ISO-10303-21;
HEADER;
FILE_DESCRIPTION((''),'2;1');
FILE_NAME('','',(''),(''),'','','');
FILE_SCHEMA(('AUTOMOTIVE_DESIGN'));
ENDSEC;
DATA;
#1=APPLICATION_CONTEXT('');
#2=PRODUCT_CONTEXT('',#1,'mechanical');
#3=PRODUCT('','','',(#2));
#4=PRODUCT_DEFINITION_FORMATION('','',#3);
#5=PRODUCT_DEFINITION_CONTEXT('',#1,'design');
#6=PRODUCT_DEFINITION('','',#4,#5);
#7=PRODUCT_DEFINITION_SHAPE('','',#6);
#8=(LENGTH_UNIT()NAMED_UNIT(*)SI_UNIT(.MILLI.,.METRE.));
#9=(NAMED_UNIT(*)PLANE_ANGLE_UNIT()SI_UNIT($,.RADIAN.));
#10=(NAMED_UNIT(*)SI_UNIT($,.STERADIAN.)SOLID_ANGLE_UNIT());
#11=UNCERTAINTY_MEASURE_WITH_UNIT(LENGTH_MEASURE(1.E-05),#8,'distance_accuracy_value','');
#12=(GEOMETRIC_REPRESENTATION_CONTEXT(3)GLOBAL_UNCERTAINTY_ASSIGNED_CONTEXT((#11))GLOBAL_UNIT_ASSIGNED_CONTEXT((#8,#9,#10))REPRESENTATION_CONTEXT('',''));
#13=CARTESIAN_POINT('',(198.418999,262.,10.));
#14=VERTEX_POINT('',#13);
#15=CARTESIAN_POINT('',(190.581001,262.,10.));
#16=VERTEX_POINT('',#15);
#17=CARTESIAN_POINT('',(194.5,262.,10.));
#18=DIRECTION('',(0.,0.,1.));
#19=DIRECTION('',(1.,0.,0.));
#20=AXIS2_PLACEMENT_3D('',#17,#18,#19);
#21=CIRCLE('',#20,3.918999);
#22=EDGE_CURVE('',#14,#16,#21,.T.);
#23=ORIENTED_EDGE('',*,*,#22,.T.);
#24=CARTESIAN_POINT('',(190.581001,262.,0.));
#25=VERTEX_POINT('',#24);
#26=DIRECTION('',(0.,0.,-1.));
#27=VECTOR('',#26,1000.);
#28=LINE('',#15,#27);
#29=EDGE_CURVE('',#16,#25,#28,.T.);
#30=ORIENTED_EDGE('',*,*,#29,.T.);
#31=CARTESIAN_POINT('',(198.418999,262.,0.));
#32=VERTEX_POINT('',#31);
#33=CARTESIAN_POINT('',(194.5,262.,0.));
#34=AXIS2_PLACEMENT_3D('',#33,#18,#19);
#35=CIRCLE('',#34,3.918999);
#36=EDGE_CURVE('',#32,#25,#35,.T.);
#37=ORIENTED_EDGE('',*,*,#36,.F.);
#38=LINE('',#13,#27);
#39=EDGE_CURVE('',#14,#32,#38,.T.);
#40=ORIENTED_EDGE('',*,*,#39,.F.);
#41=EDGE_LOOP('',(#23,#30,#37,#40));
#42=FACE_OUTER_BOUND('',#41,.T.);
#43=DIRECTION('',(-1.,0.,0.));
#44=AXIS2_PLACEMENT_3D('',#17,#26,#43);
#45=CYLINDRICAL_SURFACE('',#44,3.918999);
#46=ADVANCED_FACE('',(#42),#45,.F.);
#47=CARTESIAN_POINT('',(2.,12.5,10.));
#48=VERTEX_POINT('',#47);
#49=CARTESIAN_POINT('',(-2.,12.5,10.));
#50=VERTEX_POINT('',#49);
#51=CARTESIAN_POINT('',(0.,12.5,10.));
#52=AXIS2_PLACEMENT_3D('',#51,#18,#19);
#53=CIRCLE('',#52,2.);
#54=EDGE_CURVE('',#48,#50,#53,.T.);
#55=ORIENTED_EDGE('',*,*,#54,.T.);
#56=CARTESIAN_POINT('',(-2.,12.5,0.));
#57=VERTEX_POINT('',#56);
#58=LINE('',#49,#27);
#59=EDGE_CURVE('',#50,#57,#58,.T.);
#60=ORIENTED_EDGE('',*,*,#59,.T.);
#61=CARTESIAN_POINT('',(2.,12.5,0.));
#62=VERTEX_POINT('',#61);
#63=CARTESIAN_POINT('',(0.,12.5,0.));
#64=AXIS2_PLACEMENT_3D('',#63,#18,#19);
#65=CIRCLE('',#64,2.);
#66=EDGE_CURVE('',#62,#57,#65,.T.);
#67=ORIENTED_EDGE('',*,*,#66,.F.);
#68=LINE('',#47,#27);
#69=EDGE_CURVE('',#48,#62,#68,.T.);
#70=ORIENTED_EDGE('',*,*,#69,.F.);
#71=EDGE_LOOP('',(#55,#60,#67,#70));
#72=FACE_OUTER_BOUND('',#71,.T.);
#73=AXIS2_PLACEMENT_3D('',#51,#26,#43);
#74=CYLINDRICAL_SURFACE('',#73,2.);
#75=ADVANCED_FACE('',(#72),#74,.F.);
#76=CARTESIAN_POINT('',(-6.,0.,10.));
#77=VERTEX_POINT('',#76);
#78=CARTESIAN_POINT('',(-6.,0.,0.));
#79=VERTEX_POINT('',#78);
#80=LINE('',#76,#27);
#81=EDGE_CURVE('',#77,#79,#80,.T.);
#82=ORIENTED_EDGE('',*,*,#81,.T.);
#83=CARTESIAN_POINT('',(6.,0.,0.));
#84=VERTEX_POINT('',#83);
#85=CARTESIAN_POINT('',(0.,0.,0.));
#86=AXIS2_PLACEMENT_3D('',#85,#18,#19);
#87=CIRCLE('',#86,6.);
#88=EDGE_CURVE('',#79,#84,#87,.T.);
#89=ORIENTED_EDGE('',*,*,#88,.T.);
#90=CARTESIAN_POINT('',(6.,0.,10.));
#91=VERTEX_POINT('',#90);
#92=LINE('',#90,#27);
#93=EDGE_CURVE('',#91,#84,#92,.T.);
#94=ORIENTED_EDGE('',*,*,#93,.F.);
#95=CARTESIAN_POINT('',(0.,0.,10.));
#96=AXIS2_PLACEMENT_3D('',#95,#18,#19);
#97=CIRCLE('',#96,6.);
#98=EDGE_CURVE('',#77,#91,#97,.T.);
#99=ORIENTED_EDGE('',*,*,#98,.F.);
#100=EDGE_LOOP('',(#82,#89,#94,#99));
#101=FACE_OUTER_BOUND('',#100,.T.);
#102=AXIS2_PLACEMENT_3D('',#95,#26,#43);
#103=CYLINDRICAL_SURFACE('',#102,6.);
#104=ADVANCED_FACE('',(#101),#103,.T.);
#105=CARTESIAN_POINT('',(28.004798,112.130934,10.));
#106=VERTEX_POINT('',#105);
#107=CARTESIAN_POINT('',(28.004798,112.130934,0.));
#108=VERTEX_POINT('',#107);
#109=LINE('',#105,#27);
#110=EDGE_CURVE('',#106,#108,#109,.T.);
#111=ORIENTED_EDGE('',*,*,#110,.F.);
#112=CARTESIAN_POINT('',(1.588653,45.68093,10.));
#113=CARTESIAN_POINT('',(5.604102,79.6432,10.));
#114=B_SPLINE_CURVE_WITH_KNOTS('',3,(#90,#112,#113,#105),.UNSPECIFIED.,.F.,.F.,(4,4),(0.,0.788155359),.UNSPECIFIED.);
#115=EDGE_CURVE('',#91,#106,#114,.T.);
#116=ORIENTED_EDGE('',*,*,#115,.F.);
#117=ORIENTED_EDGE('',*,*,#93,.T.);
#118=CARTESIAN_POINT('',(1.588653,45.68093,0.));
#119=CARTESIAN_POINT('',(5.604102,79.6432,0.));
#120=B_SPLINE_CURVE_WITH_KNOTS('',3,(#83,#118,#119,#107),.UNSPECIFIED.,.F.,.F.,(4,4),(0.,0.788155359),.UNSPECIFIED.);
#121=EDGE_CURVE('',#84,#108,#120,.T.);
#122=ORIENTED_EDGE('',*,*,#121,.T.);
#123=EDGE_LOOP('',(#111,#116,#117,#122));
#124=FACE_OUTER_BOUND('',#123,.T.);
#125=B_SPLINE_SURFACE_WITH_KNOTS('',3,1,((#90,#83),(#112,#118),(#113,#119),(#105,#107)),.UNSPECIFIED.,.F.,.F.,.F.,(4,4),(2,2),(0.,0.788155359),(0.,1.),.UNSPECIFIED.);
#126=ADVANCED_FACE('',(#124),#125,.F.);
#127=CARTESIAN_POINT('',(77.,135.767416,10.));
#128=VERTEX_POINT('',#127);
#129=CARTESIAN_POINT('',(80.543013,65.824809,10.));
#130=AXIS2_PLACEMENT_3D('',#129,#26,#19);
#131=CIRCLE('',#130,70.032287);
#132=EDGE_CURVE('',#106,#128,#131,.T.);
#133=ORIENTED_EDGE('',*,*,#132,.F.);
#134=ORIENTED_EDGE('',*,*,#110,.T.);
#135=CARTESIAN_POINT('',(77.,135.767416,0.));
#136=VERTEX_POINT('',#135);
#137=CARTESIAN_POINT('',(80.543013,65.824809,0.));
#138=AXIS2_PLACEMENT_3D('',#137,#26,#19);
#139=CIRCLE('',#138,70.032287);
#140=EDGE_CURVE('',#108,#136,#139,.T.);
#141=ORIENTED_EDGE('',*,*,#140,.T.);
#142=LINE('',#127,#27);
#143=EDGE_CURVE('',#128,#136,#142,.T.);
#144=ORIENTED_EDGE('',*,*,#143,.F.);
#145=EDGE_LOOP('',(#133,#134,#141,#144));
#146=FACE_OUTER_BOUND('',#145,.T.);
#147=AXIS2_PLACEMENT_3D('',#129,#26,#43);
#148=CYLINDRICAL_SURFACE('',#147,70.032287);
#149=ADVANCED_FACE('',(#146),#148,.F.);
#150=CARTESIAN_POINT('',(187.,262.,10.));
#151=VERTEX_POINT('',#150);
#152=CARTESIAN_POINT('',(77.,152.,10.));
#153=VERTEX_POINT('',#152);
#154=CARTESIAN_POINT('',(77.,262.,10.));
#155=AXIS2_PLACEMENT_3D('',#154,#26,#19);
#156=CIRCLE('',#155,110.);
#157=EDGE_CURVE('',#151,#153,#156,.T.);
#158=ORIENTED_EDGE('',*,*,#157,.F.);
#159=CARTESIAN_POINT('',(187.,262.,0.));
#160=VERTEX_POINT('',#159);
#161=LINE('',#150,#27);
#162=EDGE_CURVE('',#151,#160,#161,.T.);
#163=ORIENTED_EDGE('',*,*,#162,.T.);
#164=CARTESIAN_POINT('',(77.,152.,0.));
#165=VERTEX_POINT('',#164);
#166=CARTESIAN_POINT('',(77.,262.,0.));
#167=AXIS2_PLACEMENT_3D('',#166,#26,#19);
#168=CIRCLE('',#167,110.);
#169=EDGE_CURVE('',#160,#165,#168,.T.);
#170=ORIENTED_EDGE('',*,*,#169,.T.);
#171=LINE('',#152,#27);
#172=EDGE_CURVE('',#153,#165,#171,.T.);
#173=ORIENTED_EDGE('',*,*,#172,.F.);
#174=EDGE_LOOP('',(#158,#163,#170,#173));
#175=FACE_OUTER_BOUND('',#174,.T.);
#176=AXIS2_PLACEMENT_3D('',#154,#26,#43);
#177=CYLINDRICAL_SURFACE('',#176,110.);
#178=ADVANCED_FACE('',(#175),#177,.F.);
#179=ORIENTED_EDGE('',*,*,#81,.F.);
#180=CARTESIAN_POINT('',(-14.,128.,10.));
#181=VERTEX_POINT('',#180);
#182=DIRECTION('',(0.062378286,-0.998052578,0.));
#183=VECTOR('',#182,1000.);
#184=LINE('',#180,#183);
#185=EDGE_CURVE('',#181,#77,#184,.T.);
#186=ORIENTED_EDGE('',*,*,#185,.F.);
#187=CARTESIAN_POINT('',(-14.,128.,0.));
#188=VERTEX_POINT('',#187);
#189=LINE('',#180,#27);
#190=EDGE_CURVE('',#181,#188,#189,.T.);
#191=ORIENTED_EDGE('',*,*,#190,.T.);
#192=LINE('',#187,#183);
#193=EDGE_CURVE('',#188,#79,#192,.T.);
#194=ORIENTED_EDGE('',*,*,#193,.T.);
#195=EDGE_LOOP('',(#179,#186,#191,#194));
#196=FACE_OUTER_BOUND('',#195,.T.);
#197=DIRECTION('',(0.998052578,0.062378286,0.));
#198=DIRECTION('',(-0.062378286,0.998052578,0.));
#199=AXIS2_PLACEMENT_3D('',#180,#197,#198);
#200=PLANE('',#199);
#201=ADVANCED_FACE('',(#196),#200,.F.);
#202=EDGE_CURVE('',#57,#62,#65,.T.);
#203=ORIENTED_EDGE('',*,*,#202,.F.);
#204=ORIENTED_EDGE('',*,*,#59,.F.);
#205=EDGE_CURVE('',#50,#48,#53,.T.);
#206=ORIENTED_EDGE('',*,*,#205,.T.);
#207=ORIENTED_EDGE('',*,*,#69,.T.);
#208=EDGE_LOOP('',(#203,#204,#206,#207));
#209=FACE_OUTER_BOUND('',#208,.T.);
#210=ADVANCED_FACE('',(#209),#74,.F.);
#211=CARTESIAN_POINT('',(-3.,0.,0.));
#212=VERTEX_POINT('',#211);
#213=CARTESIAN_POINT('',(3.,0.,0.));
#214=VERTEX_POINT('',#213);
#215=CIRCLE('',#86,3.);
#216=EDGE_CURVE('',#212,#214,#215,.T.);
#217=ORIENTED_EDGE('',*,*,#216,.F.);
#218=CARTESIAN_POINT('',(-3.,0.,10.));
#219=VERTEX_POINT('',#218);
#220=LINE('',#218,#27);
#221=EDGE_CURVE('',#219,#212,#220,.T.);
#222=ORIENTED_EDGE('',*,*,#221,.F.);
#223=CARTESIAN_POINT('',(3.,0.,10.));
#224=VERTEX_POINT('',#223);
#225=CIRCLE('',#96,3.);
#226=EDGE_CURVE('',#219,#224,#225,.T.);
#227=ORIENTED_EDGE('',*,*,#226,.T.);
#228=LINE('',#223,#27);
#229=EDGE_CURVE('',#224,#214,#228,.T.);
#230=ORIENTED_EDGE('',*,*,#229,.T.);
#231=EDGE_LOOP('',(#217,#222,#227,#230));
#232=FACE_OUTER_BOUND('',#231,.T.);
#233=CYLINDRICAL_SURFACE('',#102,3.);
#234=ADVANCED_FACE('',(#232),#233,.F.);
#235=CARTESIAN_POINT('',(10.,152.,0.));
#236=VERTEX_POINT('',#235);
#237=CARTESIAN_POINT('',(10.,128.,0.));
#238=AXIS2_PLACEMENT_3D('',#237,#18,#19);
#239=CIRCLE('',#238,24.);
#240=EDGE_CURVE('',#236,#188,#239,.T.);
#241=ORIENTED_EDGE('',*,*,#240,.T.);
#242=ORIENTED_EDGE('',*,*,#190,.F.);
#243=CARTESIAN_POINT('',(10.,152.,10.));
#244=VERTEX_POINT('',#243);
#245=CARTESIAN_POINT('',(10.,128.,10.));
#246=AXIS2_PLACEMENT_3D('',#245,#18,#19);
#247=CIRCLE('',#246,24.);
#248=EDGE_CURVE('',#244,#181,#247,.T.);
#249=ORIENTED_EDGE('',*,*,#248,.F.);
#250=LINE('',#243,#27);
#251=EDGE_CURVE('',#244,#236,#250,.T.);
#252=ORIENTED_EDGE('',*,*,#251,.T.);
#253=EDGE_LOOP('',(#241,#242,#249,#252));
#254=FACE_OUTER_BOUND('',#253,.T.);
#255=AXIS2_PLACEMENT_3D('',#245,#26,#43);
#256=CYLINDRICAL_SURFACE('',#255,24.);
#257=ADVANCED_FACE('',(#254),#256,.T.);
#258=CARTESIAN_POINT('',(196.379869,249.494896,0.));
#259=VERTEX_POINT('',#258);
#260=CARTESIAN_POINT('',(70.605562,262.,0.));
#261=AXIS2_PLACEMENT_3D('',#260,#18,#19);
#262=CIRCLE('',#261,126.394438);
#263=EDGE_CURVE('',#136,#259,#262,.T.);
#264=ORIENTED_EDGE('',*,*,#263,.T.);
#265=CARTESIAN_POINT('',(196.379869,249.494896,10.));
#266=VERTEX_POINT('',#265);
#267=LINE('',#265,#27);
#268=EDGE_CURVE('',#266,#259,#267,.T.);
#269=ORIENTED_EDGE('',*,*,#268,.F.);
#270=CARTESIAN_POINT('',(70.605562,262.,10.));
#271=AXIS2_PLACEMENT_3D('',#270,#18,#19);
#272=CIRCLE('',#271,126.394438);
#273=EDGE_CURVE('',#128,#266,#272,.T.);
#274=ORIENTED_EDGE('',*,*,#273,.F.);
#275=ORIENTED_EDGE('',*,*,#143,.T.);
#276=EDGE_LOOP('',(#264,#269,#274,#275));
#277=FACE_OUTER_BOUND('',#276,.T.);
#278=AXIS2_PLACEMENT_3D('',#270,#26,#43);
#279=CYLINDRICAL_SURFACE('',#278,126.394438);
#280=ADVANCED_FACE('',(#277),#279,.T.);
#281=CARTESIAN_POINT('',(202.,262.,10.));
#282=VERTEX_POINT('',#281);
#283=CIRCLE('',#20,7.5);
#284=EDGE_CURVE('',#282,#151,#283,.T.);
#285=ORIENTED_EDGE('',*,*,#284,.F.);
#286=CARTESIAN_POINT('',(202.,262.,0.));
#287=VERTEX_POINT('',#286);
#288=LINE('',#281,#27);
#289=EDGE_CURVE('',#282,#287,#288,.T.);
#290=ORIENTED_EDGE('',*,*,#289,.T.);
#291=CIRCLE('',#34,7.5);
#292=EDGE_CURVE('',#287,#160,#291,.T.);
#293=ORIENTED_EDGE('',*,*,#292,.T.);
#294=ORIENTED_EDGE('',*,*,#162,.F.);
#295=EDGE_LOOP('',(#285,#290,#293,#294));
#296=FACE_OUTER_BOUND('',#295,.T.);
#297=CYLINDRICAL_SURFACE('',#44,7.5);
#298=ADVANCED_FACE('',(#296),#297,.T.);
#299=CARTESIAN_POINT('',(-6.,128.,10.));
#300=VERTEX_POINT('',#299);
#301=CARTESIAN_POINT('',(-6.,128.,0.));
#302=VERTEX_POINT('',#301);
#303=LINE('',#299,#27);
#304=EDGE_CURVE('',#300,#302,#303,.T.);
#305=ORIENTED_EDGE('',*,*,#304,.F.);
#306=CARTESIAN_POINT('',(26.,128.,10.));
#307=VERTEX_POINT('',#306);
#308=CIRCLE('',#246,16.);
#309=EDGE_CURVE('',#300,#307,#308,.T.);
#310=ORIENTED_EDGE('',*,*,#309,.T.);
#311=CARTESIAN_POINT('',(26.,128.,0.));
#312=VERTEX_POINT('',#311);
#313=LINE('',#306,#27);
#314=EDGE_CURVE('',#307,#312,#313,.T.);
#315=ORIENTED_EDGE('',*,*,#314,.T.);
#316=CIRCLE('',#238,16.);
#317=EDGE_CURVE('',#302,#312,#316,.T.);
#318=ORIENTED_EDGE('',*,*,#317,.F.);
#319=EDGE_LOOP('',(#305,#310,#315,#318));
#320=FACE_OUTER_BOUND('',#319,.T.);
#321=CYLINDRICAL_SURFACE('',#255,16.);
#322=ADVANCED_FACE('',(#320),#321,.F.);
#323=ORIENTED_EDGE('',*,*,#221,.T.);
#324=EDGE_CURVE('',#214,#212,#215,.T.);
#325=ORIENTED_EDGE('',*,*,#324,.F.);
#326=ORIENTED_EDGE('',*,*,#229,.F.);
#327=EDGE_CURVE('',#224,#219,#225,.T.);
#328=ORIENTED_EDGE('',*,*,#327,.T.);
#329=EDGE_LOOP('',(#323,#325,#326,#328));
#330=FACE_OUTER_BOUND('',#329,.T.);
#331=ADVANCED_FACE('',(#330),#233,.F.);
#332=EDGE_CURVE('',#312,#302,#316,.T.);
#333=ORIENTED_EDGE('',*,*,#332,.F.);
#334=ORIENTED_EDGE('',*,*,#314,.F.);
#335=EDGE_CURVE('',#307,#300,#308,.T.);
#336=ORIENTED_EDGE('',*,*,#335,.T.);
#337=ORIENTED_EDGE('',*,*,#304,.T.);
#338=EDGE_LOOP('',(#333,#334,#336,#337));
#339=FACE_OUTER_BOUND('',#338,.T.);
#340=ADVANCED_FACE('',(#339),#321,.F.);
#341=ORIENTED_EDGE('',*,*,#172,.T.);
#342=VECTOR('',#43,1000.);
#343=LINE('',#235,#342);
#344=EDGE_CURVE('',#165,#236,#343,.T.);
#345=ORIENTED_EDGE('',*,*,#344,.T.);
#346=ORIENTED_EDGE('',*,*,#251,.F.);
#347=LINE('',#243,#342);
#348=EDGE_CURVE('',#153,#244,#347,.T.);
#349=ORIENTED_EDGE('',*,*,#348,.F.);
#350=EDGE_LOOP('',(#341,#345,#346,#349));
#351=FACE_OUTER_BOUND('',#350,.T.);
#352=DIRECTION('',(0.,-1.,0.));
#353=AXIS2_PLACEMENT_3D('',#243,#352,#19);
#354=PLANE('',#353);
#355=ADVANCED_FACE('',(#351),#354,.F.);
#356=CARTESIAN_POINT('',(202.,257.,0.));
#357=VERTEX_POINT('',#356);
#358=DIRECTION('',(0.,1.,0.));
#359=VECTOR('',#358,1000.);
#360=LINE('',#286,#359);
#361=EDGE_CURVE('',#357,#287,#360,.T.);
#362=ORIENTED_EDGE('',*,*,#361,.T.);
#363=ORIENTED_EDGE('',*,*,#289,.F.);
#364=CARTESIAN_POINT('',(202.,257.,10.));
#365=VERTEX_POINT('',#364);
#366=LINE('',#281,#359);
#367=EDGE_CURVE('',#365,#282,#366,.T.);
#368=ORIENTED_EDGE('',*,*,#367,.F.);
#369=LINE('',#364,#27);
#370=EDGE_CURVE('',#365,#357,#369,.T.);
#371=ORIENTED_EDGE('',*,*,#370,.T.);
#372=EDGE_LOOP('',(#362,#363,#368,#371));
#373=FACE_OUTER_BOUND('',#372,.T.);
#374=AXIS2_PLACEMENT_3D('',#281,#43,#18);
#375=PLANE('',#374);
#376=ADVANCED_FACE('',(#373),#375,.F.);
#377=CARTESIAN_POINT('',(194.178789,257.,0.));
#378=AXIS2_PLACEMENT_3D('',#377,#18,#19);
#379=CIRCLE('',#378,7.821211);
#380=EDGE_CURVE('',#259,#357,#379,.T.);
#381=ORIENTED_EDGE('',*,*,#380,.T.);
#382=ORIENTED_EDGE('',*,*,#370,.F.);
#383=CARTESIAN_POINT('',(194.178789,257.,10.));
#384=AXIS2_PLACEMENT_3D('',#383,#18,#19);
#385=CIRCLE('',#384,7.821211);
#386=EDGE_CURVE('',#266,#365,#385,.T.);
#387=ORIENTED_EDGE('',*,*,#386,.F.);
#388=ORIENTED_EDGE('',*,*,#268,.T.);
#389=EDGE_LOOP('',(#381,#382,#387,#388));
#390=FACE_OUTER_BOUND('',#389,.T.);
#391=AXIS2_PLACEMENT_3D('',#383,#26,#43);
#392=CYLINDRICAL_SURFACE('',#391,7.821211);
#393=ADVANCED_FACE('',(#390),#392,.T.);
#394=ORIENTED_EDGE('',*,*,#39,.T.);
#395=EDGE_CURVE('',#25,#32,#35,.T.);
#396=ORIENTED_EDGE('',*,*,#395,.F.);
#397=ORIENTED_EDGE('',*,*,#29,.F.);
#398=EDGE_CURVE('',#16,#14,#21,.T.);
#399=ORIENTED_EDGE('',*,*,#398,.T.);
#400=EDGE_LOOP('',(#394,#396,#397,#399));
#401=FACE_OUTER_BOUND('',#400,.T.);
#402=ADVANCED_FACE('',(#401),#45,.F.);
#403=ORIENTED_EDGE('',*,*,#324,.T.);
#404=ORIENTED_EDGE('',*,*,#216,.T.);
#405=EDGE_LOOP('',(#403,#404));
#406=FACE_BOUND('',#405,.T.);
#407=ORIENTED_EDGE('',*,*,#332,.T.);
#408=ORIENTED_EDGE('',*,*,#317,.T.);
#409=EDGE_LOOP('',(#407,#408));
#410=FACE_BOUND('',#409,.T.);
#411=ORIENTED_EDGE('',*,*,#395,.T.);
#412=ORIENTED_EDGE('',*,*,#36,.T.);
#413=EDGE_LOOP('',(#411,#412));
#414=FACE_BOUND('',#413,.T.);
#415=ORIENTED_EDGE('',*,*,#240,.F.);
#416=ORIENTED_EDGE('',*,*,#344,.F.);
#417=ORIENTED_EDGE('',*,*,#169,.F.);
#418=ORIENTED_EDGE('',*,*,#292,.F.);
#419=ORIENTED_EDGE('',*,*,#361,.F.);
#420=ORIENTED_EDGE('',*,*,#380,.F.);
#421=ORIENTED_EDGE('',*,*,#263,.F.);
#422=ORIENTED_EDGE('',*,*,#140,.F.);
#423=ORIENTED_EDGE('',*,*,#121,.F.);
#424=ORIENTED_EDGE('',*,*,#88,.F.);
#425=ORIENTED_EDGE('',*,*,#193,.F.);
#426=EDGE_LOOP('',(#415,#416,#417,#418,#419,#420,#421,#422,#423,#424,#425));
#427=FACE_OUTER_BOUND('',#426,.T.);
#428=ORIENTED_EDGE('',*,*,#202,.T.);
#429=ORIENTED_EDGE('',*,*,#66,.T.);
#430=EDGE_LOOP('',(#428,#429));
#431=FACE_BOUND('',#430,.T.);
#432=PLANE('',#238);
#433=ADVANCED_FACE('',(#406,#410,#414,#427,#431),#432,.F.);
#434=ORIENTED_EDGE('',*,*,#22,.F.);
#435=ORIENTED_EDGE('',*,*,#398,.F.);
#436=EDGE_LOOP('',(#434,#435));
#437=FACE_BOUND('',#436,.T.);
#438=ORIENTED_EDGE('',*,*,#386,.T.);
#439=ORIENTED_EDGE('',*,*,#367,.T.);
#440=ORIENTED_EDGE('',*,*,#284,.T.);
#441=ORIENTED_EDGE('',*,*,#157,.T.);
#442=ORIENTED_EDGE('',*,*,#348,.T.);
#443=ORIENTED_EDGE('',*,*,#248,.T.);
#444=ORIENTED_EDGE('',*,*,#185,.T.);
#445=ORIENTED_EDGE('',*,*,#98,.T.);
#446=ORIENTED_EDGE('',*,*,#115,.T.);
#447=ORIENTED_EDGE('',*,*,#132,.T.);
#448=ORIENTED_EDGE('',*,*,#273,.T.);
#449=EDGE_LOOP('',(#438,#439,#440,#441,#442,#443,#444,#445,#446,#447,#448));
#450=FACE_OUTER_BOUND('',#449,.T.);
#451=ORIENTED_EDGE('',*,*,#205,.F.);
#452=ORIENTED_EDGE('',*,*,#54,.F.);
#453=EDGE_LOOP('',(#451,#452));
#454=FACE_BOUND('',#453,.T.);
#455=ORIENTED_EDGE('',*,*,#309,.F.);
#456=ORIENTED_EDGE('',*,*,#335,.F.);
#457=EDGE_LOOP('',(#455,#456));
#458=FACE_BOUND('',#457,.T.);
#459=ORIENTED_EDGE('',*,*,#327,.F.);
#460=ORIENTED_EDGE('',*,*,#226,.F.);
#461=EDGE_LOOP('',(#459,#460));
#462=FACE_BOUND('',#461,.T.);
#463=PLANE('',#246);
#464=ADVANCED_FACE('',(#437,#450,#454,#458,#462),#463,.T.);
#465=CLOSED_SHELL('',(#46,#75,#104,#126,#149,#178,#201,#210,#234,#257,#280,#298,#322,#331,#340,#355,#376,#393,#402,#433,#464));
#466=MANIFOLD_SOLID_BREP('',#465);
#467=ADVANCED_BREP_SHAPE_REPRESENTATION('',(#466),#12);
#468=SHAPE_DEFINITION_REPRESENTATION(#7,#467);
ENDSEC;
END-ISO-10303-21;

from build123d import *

# Parameters (mm, degrees)
SKETCH_1_R      = 3
SKETCH_1_R_2    = 16
SKETCH_1_R_3    = 3.91899873
SKETCH_1_R_4    = 2
EXTRUDE_1_DEPTH = 10


with BuildPart() as part:
    # 草图1 → 凸台-拉伸1 (new body)
    with BuildSketch(Plane.XY):
        with BuildLine():
            Line((-14, 128), (-6, 0))
            ThreePointArc((-6, 0), (0, -6), (6, 0))
            add(Edge.make_bspline(
                [(6, 0), (1.588652615, 45.680929706), (5.604102499, 79.643200211), (28.004797731, 112.13093391)],
                knots=[0, 0, 0, 0, 0.788155359, 0.788155359, 0.788155359, 0.788155359], degree=3))
            ThreePointArc((28.004797731, 112.13093391), (50.113637924, 128.900750568), (77, 135.767416406))
            ThreePointArc((77, 135.767416406), (157.787149523, 170.485384951), (196.379869136, 249.494896157))
            ThreePointArc((196.379869136, 249.494896157), (200.439238403, 252.311917913), (202, 257))
            Line((202, 257), (202, 262))
            ThreePointArc((202, 262), (194.5, 269.5), (187, 262))
            ThreePointArc((187, 262), (154.781745931, 184.218254069), (77, 152))
            Line((77, 152), (10, 152))
            ThreePointArc((10, 152), (-6.970562748, 144.970562748), (-14, 128))
        make_face()
        Circle(SKETCH_1_R, mode=Mode.SUBTRACT)
        with Locations((10, 128)):
            Circle(SKETCH_1_R_2, mode=Mode.SUBTRACT)
        with Locations((194.5, 262)):
            Circle(SKETCH_1_R_3, mode=Mode.SUBTRACT)
        with Locations((0, 12.5)):
            Circle(SKETCH_1_R_4, mode=Mode.SUBTRACT)
    extrude(amount=EXTRUDE_1_DEPTH)


solid = part.part
